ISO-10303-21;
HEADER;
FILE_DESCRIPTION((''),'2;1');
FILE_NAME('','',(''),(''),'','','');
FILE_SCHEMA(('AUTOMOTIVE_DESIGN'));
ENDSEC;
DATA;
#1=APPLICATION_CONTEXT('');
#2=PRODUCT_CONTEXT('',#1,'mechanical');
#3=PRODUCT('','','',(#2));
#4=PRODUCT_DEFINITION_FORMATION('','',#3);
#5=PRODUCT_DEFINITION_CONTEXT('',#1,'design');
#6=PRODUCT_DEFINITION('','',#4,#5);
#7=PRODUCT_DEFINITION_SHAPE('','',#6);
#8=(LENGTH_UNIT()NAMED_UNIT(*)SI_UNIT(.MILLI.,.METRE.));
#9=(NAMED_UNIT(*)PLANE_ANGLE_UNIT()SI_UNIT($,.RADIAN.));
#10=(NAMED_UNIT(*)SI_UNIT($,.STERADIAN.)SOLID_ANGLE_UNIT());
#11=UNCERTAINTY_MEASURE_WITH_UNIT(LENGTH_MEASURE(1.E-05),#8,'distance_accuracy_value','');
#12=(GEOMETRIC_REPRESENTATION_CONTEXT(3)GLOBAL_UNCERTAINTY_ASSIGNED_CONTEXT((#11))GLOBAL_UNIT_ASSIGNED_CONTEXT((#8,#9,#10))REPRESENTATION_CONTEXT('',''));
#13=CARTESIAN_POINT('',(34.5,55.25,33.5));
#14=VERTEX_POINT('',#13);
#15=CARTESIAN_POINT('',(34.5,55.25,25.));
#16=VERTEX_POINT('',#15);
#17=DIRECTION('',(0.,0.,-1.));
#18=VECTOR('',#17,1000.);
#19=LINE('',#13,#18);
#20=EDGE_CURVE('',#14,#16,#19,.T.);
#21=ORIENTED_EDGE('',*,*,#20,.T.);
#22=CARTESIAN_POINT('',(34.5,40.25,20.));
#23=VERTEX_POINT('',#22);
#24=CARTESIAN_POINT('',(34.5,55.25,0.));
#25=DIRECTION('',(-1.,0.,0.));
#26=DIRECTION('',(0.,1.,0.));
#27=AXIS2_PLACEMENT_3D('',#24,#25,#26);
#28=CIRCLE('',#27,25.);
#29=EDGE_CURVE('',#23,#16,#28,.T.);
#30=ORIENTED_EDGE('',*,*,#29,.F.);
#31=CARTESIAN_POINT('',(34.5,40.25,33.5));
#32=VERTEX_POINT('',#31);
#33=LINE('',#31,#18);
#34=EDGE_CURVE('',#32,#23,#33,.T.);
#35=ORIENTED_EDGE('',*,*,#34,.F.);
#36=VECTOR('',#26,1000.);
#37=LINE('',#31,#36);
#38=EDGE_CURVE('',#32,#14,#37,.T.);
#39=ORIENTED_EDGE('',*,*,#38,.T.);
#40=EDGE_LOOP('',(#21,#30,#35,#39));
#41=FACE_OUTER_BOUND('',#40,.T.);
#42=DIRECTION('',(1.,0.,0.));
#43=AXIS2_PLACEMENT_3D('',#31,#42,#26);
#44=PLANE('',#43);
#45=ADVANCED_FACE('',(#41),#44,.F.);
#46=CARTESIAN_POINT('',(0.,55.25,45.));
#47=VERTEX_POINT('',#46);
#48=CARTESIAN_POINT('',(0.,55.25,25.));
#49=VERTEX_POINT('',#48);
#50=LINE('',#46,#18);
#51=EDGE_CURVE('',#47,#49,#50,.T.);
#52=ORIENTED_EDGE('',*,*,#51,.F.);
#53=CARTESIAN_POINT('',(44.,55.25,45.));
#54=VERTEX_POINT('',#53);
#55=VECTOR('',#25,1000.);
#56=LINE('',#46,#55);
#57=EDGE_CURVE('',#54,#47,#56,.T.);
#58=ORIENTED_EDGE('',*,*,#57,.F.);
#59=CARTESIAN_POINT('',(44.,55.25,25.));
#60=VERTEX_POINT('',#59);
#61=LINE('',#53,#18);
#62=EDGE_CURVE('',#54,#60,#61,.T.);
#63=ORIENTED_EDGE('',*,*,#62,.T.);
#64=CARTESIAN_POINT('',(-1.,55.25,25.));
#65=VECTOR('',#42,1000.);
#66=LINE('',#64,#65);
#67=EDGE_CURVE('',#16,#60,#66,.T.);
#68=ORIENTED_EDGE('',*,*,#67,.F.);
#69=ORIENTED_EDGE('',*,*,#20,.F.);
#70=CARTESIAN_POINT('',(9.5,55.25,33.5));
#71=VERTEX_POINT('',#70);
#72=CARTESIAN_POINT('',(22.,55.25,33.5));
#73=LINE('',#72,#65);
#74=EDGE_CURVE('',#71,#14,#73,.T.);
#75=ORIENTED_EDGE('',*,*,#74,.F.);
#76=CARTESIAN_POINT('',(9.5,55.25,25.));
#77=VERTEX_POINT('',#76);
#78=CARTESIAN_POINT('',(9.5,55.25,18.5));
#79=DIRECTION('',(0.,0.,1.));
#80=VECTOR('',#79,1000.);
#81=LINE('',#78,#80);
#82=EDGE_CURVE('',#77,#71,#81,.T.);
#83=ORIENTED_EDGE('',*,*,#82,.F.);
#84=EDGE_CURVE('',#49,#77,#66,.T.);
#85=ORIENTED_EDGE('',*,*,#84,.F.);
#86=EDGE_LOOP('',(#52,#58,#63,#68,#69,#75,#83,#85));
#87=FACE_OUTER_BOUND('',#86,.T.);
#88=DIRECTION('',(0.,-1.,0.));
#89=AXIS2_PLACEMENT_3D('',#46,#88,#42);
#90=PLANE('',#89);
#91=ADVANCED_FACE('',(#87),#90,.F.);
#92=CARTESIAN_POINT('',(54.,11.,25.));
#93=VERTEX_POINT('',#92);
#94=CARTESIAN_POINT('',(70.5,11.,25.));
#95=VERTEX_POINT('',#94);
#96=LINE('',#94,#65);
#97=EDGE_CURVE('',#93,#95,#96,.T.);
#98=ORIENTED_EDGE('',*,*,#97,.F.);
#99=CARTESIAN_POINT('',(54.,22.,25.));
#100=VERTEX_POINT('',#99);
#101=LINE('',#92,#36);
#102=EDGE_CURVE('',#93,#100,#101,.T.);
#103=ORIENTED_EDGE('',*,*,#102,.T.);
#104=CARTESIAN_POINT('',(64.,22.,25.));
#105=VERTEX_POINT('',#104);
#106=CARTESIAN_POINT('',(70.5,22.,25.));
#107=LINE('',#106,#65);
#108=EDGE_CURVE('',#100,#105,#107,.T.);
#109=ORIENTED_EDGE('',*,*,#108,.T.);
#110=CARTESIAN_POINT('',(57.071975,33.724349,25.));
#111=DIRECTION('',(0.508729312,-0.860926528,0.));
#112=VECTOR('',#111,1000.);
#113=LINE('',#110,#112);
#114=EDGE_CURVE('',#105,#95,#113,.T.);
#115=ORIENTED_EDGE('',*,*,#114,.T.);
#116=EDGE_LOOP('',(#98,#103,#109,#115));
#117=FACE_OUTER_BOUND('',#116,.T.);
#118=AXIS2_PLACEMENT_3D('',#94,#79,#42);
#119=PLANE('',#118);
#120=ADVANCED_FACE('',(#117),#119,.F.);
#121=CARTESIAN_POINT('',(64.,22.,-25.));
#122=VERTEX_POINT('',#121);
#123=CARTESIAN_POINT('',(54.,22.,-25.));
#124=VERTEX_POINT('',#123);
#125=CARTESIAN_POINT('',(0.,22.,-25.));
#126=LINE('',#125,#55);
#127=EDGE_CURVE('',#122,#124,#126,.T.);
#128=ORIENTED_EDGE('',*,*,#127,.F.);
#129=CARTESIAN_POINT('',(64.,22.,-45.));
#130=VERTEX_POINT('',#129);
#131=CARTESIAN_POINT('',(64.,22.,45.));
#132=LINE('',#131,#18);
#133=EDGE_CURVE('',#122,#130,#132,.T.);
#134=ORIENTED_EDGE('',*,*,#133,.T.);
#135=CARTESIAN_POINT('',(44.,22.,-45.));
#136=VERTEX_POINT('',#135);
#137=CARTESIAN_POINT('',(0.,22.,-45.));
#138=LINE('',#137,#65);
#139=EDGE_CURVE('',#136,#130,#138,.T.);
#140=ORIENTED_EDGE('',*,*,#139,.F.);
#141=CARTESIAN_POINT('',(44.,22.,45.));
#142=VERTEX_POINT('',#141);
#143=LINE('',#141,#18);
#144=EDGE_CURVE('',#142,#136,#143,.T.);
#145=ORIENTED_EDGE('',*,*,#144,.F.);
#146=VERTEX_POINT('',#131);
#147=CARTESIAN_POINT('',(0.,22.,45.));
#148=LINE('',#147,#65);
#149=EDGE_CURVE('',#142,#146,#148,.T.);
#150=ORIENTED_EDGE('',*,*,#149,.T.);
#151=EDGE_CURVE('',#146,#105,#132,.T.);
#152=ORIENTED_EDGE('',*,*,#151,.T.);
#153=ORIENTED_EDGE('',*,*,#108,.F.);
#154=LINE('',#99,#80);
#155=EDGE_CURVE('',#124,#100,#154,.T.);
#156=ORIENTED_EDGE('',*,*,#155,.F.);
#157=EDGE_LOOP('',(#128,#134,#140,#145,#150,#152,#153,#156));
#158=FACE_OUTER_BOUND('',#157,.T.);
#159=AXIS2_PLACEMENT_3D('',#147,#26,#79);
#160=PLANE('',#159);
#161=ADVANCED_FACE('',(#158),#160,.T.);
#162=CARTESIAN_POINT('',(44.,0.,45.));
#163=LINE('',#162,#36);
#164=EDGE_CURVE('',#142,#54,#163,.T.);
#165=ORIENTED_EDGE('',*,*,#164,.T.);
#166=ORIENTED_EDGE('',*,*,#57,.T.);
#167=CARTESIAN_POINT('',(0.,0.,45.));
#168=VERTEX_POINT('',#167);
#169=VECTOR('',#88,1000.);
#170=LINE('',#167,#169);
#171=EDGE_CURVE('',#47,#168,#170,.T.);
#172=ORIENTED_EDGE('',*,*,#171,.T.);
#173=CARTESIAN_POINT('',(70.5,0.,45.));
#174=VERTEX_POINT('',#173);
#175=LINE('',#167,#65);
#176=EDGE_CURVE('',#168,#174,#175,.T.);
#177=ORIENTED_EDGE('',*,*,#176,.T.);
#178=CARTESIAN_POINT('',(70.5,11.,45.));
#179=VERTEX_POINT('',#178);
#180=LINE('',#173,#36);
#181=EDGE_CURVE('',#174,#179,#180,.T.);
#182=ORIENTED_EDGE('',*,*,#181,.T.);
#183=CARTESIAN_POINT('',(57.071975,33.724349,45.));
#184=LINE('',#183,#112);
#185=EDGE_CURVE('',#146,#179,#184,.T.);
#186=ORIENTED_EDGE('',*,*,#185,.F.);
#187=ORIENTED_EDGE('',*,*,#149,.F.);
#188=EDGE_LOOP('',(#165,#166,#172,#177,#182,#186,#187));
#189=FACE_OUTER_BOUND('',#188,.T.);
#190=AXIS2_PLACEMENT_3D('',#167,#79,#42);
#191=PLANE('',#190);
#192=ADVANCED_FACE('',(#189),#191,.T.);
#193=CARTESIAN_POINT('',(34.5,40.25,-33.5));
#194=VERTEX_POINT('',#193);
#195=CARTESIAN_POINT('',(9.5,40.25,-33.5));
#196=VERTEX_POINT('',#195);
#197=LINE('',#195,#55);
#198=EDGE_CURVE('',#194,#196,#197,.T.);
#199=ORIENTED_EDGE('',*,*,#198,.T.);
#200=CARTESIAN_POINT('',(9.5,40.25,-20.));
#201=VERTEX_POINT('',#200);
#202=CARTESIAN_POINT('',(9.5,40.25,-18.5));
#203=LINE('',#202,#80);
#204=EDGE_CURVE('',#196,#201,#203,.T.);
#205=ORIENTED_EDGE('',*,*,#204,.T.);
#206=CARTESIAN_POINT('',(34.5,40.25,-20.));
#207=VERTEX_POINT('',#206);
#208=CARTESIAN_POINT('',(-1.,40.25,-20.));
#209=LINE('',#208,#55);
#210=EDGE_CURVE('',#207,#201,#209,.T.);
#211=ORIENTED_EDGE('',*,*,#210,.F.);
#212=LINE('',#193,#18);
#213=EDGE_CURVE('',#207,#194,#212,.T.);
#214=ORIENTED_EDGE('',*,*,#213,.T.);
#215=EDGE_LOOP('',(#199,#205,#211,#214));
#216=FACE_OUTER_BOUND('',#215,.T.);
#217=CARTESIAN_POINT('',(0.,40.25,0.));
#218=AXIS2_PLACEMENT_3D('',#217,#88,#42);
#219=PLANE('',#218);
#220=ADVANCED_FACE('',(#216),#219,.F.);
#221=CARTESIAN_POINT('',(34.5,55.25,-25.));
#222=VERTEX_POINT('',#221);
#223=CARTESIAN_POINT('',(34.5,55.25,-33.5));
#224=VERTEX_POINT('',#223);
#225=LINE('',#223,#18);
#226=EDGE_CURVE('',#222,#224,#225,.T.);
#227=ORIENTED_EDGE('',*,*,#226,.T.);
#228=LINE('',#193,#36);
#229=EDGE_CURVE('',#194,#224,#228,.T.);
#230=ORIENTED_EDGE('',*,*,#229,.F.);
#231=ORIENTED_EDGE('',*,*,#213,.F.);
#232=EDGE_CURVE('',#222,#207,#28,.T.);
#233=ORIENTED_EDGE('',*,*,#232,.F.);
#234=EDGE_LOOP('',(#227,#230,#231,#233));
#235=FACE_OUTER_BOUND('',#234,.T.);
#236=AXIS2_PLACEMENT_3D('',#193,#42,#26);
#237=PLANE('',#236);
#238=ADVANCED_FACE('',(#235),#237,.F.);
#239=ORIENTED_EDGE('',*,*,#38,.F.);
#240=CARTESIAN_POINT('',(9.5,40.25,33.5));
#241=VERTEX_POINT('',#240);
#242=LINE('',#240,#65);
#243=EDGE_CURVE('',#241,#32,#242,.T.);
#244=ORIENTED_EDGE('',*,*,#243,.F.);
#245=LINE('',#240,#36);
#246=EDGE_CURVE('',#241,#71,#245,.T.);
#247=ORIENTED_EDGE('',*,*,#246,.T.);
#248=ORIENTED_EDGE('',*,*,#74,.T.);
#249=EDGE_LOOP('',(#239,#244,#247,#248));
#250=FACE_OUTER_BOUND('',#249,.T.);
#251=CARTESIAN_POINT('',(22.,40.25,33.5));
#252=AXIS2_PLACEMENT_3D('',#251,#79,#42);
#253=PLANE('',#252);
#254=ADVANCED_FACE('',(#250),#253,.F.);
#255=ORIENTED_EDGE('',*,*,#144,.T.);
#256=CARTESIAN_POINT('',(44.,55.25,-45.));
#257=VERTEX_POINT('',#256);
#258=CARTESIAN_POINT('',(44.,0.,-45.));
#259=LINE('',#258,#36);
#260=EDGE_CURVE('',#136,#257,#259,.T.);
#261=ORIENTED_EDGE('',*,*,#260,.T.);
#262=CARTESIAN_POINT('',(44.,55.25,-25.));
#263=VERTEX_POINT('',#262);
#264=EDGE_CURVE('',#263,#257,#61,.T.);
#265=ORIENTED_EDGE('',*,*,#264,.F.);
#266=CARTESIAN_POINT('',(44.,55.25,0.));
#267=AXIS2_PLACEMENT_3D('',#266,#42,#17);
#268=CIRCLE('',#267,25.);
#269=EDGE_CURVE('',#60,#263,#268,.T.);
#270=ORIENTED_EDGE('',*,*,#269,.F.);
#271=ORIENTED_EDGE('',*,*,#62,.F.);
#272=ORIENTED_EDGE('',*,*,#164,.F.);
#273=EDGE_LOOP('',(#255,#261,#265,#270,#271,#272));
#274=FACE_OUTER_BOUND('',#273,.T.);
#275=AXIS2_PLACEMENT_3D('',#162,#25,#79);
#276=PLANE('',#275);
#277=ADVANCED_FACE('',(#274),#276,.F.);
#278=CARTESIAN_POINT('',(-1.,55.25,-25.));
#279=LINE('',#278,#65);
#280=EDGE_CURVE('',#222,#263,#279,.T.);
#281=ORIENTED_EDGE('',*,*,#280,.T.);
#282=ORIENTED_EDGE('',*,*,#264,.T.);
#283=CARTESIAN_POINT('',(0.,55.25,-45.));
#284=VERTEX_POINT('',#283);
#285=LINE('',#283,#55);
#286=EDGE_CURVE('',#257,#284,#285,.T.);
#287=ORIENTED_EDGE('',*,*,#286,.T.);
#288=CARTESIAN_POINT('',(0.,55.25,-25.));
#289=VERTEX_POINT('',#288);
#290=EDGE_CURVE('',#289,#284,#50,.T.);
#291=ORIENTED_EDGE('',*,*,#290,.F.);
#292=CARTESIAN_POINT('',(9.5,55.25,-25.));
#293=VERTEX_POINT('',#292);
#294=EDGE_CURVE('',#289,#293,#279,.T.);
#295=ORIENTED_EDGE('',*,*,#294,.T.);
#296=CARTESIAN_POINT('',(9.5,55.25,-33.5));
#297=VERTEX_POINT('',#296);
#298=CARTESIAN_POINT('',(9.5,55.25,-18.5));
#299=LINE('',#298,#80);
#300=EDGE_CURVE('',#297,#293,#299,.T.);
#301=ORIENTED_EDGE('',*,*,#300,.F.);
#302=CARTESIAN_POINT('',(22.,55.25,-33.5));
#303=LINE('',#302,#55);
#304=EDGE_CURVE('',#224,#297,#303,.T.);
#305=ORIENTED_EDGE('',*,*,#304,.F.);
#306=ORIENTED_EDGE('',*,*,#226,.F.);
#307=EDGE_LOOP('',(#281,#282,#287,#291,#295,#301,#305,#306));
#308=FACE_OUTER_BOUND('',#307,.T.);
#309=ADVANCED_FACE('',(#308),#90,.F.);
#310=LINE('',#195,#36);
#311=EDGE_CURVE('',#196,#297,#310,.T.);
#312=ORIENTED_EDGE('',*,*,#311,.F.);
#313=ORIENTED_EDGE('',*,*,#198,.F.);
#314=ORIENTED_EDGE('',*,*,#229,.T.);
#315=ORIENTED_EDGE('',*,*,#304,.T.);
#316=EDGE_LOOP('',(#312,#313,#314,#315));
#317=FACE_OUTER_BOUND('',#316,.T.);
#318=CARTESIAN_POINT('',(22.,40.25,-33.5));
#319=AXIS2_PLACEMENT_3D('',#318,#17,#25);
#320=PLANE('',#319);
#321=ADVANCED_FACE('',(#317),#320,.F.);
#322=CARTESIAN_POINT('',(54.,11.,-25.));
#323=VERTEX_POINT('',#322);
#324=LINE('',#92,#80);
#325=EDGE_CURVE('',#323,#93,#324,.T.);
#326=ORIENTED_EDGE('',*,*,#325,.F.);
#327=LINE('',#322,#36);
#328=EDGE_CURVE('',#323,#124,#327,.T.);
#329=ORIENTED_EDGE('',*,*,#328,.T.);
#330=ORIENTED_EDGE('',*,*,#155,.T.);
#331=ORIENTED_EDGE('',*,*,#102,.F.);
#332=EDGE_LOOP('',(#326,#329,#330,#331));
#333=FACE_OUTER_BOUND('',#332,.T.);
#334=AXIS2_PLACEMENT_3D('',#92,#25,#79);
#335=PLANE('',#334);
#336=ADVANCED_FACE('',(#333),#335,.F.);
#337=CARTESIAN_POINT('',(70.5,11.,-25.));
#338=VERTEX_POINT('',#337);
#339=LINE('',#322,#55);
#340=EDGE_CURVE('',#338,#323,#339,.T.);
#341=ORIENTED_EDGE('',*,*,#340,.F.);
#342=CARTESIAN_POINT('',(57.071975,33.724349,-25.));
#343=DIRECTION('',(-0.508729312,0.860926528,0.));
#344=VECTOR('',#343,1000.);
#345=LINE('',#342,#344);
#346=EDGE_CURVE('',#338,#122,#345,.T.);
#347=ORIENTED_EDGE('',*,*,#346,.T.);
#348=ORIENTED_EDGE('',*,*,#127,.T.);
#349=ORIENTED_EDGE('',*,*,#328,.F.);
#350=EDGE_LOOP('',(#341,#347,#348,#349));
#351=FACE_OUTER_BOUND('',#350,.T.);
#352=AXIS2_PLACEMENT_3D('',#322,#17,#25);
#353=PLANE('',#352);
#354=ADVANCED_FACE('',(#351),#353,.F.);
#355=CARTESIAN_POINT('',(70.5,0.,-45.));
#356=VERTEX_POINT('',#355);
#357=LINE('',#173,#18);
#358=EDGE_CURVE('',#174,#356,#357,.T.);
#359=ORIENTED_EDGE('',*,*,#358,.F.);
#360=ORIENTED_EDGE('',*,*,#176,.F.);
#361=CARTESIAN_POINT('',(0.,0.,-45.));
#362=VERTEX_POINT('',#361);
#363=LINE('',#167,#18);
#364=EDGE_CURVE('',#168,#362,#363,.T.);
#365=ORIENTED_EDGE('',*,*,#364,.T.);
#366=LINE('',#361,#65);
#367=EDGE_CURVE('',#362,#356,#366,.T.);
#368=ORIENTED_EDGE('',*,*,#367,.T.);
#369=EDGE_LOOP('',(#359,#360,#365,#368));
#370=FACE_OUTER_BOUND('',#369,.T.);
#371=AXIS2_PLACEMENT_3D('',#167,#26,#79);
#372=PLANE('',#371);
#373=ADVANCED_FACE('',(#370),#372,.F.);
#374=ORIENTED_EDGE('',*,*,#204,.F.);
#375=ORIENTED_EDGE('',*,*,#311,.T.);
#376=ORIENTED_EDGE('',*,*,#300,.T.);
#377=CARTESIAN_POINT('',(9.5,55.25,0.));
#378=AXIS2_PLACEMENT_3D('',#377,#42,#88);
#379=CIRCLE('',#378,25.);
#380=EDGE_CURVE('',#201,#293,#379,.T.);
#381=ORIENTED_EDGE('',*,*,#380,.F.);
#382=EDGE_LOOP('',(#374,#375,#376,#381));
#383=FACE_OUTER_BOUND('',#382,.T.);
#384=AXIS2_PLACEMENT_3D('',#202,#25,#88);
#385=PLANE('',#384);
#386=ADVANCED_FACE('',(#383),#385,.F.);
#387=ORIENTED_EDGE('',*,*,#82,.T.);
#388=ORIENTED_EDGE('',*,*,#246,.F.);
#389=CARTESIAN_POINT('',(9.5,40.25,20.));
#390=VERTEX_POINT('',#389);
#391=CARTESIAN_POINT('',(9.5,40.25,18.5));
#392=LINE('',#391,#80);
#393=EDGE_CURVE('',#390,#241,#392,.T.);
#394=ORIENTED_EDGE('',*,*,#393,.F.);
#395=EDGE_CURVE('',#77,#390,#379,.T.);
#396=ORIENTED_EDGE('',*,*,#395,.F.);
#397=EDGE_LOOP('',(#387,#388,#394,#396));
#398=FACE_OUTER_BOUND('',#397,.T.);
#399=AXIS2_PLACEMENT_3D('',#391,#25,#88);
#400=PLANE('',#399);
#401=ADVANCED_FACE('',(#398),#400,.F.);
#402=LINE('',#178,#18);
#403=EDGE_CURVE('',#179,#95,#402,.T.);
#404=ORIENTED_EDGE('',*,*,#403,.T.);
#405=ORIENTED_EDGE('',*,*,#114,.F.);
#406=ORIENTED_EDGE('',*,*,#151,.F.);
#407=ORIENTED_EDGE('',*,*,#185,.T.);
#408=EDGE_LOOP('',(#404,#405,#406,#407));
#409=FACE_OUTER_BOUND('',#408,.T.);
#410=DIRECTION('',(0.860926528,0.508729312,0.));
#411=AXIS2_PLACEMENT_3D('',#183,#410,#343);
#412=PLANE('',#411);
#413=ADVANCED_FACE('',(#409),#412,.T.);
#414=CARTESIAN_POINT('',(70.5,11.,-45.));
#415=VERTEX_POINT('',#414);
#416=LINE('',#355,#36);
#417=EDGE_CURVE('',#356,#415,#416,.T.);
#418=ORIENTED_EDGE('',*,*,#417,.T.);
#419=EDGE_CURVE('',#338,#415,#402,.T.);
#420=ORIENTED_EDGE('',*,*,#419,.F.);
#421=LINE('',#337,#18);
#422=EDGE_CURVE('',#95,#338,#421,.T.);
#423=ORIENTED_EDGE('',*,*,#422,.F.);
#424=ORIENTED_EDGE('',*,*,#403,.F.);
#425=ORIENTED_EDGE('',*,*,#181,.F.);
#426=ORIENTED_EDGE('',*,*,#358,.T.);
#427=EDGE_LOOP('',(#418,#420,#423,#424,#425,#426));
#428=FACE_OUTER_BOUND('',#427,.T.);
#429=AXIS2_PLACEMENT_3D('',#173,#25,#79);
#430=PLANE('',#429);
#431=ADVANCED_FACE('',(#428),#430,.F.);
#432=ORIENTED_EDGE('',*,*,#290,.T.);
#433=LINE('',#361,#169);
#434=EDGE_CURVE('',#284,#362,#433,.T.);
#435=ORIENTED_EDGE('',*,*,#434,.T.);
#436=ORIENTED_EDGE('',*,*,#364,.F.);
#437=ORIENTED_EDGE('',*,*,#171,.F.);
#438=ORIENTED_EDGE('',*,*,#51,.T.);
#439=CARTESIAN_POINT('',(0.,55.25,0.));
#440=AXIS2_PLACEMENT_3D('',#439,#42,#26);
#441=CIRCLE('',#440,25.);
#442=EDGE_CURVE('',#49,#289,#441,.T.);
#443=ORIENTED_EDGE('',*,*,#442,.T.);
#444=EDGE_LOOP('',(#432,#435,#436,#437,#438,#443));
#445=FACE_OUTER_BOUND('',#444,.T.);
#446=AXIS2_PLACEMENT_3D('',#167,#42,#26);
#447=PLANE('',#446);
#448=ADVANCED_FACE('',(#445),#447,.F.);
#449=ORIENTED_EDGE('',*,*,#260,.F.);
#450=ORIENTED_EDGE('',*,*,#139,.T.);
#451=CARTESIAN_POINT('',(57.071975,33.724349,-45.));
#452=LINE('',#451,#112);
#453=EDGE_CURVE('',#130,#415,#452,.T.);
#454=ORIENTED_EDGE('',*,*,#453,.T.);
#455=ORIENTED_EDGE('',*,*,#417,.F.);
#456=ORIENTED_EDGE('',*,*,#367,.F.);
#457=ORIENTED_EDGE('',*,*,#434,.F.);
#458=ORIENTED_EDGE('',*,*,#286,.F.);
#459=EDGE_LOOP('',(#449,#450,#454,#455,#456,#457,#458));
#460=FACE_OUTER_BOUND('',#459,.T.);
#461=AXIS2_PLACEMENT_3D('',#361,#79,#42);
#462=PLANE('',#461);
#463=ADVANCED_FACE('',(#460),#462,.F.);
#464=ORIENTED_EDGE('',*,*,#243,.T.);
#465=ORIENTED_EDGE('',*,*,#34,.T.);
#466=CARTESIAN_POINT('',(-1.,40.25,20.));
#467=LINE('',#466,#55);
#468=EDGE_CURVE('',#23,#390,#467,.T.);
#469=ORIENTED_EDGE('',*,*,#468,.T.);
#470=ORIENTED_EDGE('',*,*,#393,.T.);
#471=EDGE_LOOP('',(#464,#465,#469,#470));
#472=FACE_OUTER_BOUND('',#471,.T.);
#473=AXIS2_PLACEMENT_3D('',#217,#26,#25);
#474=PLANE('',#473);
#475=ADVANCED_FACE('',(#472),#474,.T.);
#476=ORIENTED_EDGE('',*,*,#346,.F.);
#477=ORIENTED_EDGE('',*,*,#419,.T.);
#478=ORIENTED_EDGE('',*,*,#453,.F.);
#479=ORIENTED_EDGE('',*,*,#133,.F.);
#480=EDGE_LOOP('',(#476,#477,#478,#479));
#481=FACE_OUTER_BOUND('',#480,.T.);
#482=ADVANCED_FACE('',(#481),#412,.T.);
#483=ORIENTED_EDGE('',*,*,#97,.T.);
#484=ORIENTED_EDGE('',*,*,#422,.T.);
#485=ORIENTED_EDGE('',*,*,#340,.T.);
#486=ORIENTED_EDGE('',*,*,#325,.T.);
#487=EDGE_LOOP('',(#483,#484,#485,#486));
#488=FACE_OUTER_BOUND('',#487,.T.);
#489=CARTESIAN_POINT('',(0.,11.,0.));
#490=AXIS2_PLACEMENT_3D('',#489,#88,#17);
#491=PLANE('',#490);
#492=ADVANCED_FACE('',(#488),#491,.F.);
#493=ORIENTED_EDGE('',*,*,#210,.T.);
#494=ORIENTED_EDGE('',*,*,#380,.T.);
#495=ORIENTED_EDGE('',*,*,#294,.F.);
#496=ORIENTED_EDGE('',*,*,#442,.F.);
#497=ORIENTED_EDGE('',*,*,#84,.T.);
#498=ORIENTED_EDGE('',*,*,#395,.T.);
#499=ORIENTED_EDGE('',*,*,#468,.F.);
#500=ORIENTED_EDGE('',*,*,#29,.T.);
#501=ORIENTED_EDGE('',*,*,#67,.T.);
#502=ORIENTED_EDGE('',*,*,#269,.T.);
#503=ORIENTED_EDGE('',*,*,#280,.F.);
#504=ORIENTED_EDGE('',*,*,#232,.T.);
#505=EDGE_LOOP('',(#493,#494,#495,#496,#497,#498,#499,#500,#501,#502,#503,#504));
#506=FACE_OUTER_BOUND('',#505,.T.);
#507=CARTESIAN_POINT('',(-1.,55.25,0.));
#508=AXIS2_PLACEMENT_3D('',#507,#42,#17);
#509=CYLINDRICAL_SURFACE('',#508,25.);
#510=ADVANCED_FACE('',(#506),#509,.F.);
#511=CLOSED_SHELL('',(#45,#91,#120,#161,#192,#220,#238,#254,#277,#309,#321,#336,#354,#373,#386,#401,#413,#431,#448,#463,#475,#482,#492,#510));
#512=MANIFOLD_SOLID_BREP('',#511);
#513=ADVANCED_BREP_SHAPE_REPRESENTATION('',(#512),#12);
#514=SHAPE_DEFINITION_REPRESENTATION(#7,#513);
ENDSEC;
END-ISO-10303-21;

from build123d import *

# Parameters (mm, degrees)
BRACKET_PROFILE_SKETCH_W = 44
BRACKET_PROFILE_SKETCH_H = 55.25
BRACKET_BODY_DEPTH       = 45
BEARING_SEAT_R25_DEPTH   = 45
BASE_SLOT_SKETCH_W       = 16.5
BASE_SLOT_SKETCH_H       = 50
BASE_MOUNTING_SLOT_DEPTH = 11
TOP_RECESSES_DEPTH       = 15


with BuildPart() as part:
    # Bracket Profile Sketch → Bracket Body (new, symmetric)
    with BuildSketch(Plane.XY):
        with Locations((22, 27.625)):
            Rectangle(BRACKET_PROFILE_SKETCH_W, BRACKET_PROFILE_SKETCH_H)
        Polygon((44, 22), (44, 0), (70.5, 0), (70.5, 11), (64, 22), align=None)
    extrude(amount=BRACKET_BODY_DEPTH, both=True)

    # Bearing Seat Sketch → Bearing Seat R25 (cut)
    with BuildSketch(Plane(origin=(44, 0, 0), x_dir=(0, 0, -1), z_dir=(1, 0, 0))):
        with BuildLine():
            Line((-25, 55.25), (25, 55.25))
            ThreePointArc((25, 55.25), (0, 30.25), (-25, 55.25))
        make_face()
    extrude(amount=-BEARING_SEAT_R25_DEPTH, mode=Mode.SUBTRACT)

    # Base Slot Sketch → Base Mounting Slot (cut)
    with BuildSketch(Plane(origin=(0, 22, 0), x_dir=(1, 0, 0), z_dir=(0, 1, 0))):
        with Locations((62.25, 0)):
            Rectangle(BASE_SLOT_SKETCH_W, BASE_SLOT_SKETCH_H)
    extrude(amount=-BASE_MOUNTING_SLOT_DEPTH, mode=Mode.SUBTRACT)

    # Top Recess Sketch → Top Recesses (cut)
    with BuildSketch(Plane(origin=(0, 55.25, 0), x_dir=(1, 0, 0), z_dir=(0, 1, 0))):
        Polygon((9.5, -33.5), (22, -33.5), (34.5, -33.5), (34.5, -18.5), (9.5, -18.5), align=None)
        Polygon((22, 33.5), (34.5, 33.5), (34.5, 18.5), (9.5, 18.5), (9.5, 33.5), align=None)
    extrude(amount=-TOP_RECESSES_DEPTH, mode=Mode.SUBTRACT)


solid = part.part
